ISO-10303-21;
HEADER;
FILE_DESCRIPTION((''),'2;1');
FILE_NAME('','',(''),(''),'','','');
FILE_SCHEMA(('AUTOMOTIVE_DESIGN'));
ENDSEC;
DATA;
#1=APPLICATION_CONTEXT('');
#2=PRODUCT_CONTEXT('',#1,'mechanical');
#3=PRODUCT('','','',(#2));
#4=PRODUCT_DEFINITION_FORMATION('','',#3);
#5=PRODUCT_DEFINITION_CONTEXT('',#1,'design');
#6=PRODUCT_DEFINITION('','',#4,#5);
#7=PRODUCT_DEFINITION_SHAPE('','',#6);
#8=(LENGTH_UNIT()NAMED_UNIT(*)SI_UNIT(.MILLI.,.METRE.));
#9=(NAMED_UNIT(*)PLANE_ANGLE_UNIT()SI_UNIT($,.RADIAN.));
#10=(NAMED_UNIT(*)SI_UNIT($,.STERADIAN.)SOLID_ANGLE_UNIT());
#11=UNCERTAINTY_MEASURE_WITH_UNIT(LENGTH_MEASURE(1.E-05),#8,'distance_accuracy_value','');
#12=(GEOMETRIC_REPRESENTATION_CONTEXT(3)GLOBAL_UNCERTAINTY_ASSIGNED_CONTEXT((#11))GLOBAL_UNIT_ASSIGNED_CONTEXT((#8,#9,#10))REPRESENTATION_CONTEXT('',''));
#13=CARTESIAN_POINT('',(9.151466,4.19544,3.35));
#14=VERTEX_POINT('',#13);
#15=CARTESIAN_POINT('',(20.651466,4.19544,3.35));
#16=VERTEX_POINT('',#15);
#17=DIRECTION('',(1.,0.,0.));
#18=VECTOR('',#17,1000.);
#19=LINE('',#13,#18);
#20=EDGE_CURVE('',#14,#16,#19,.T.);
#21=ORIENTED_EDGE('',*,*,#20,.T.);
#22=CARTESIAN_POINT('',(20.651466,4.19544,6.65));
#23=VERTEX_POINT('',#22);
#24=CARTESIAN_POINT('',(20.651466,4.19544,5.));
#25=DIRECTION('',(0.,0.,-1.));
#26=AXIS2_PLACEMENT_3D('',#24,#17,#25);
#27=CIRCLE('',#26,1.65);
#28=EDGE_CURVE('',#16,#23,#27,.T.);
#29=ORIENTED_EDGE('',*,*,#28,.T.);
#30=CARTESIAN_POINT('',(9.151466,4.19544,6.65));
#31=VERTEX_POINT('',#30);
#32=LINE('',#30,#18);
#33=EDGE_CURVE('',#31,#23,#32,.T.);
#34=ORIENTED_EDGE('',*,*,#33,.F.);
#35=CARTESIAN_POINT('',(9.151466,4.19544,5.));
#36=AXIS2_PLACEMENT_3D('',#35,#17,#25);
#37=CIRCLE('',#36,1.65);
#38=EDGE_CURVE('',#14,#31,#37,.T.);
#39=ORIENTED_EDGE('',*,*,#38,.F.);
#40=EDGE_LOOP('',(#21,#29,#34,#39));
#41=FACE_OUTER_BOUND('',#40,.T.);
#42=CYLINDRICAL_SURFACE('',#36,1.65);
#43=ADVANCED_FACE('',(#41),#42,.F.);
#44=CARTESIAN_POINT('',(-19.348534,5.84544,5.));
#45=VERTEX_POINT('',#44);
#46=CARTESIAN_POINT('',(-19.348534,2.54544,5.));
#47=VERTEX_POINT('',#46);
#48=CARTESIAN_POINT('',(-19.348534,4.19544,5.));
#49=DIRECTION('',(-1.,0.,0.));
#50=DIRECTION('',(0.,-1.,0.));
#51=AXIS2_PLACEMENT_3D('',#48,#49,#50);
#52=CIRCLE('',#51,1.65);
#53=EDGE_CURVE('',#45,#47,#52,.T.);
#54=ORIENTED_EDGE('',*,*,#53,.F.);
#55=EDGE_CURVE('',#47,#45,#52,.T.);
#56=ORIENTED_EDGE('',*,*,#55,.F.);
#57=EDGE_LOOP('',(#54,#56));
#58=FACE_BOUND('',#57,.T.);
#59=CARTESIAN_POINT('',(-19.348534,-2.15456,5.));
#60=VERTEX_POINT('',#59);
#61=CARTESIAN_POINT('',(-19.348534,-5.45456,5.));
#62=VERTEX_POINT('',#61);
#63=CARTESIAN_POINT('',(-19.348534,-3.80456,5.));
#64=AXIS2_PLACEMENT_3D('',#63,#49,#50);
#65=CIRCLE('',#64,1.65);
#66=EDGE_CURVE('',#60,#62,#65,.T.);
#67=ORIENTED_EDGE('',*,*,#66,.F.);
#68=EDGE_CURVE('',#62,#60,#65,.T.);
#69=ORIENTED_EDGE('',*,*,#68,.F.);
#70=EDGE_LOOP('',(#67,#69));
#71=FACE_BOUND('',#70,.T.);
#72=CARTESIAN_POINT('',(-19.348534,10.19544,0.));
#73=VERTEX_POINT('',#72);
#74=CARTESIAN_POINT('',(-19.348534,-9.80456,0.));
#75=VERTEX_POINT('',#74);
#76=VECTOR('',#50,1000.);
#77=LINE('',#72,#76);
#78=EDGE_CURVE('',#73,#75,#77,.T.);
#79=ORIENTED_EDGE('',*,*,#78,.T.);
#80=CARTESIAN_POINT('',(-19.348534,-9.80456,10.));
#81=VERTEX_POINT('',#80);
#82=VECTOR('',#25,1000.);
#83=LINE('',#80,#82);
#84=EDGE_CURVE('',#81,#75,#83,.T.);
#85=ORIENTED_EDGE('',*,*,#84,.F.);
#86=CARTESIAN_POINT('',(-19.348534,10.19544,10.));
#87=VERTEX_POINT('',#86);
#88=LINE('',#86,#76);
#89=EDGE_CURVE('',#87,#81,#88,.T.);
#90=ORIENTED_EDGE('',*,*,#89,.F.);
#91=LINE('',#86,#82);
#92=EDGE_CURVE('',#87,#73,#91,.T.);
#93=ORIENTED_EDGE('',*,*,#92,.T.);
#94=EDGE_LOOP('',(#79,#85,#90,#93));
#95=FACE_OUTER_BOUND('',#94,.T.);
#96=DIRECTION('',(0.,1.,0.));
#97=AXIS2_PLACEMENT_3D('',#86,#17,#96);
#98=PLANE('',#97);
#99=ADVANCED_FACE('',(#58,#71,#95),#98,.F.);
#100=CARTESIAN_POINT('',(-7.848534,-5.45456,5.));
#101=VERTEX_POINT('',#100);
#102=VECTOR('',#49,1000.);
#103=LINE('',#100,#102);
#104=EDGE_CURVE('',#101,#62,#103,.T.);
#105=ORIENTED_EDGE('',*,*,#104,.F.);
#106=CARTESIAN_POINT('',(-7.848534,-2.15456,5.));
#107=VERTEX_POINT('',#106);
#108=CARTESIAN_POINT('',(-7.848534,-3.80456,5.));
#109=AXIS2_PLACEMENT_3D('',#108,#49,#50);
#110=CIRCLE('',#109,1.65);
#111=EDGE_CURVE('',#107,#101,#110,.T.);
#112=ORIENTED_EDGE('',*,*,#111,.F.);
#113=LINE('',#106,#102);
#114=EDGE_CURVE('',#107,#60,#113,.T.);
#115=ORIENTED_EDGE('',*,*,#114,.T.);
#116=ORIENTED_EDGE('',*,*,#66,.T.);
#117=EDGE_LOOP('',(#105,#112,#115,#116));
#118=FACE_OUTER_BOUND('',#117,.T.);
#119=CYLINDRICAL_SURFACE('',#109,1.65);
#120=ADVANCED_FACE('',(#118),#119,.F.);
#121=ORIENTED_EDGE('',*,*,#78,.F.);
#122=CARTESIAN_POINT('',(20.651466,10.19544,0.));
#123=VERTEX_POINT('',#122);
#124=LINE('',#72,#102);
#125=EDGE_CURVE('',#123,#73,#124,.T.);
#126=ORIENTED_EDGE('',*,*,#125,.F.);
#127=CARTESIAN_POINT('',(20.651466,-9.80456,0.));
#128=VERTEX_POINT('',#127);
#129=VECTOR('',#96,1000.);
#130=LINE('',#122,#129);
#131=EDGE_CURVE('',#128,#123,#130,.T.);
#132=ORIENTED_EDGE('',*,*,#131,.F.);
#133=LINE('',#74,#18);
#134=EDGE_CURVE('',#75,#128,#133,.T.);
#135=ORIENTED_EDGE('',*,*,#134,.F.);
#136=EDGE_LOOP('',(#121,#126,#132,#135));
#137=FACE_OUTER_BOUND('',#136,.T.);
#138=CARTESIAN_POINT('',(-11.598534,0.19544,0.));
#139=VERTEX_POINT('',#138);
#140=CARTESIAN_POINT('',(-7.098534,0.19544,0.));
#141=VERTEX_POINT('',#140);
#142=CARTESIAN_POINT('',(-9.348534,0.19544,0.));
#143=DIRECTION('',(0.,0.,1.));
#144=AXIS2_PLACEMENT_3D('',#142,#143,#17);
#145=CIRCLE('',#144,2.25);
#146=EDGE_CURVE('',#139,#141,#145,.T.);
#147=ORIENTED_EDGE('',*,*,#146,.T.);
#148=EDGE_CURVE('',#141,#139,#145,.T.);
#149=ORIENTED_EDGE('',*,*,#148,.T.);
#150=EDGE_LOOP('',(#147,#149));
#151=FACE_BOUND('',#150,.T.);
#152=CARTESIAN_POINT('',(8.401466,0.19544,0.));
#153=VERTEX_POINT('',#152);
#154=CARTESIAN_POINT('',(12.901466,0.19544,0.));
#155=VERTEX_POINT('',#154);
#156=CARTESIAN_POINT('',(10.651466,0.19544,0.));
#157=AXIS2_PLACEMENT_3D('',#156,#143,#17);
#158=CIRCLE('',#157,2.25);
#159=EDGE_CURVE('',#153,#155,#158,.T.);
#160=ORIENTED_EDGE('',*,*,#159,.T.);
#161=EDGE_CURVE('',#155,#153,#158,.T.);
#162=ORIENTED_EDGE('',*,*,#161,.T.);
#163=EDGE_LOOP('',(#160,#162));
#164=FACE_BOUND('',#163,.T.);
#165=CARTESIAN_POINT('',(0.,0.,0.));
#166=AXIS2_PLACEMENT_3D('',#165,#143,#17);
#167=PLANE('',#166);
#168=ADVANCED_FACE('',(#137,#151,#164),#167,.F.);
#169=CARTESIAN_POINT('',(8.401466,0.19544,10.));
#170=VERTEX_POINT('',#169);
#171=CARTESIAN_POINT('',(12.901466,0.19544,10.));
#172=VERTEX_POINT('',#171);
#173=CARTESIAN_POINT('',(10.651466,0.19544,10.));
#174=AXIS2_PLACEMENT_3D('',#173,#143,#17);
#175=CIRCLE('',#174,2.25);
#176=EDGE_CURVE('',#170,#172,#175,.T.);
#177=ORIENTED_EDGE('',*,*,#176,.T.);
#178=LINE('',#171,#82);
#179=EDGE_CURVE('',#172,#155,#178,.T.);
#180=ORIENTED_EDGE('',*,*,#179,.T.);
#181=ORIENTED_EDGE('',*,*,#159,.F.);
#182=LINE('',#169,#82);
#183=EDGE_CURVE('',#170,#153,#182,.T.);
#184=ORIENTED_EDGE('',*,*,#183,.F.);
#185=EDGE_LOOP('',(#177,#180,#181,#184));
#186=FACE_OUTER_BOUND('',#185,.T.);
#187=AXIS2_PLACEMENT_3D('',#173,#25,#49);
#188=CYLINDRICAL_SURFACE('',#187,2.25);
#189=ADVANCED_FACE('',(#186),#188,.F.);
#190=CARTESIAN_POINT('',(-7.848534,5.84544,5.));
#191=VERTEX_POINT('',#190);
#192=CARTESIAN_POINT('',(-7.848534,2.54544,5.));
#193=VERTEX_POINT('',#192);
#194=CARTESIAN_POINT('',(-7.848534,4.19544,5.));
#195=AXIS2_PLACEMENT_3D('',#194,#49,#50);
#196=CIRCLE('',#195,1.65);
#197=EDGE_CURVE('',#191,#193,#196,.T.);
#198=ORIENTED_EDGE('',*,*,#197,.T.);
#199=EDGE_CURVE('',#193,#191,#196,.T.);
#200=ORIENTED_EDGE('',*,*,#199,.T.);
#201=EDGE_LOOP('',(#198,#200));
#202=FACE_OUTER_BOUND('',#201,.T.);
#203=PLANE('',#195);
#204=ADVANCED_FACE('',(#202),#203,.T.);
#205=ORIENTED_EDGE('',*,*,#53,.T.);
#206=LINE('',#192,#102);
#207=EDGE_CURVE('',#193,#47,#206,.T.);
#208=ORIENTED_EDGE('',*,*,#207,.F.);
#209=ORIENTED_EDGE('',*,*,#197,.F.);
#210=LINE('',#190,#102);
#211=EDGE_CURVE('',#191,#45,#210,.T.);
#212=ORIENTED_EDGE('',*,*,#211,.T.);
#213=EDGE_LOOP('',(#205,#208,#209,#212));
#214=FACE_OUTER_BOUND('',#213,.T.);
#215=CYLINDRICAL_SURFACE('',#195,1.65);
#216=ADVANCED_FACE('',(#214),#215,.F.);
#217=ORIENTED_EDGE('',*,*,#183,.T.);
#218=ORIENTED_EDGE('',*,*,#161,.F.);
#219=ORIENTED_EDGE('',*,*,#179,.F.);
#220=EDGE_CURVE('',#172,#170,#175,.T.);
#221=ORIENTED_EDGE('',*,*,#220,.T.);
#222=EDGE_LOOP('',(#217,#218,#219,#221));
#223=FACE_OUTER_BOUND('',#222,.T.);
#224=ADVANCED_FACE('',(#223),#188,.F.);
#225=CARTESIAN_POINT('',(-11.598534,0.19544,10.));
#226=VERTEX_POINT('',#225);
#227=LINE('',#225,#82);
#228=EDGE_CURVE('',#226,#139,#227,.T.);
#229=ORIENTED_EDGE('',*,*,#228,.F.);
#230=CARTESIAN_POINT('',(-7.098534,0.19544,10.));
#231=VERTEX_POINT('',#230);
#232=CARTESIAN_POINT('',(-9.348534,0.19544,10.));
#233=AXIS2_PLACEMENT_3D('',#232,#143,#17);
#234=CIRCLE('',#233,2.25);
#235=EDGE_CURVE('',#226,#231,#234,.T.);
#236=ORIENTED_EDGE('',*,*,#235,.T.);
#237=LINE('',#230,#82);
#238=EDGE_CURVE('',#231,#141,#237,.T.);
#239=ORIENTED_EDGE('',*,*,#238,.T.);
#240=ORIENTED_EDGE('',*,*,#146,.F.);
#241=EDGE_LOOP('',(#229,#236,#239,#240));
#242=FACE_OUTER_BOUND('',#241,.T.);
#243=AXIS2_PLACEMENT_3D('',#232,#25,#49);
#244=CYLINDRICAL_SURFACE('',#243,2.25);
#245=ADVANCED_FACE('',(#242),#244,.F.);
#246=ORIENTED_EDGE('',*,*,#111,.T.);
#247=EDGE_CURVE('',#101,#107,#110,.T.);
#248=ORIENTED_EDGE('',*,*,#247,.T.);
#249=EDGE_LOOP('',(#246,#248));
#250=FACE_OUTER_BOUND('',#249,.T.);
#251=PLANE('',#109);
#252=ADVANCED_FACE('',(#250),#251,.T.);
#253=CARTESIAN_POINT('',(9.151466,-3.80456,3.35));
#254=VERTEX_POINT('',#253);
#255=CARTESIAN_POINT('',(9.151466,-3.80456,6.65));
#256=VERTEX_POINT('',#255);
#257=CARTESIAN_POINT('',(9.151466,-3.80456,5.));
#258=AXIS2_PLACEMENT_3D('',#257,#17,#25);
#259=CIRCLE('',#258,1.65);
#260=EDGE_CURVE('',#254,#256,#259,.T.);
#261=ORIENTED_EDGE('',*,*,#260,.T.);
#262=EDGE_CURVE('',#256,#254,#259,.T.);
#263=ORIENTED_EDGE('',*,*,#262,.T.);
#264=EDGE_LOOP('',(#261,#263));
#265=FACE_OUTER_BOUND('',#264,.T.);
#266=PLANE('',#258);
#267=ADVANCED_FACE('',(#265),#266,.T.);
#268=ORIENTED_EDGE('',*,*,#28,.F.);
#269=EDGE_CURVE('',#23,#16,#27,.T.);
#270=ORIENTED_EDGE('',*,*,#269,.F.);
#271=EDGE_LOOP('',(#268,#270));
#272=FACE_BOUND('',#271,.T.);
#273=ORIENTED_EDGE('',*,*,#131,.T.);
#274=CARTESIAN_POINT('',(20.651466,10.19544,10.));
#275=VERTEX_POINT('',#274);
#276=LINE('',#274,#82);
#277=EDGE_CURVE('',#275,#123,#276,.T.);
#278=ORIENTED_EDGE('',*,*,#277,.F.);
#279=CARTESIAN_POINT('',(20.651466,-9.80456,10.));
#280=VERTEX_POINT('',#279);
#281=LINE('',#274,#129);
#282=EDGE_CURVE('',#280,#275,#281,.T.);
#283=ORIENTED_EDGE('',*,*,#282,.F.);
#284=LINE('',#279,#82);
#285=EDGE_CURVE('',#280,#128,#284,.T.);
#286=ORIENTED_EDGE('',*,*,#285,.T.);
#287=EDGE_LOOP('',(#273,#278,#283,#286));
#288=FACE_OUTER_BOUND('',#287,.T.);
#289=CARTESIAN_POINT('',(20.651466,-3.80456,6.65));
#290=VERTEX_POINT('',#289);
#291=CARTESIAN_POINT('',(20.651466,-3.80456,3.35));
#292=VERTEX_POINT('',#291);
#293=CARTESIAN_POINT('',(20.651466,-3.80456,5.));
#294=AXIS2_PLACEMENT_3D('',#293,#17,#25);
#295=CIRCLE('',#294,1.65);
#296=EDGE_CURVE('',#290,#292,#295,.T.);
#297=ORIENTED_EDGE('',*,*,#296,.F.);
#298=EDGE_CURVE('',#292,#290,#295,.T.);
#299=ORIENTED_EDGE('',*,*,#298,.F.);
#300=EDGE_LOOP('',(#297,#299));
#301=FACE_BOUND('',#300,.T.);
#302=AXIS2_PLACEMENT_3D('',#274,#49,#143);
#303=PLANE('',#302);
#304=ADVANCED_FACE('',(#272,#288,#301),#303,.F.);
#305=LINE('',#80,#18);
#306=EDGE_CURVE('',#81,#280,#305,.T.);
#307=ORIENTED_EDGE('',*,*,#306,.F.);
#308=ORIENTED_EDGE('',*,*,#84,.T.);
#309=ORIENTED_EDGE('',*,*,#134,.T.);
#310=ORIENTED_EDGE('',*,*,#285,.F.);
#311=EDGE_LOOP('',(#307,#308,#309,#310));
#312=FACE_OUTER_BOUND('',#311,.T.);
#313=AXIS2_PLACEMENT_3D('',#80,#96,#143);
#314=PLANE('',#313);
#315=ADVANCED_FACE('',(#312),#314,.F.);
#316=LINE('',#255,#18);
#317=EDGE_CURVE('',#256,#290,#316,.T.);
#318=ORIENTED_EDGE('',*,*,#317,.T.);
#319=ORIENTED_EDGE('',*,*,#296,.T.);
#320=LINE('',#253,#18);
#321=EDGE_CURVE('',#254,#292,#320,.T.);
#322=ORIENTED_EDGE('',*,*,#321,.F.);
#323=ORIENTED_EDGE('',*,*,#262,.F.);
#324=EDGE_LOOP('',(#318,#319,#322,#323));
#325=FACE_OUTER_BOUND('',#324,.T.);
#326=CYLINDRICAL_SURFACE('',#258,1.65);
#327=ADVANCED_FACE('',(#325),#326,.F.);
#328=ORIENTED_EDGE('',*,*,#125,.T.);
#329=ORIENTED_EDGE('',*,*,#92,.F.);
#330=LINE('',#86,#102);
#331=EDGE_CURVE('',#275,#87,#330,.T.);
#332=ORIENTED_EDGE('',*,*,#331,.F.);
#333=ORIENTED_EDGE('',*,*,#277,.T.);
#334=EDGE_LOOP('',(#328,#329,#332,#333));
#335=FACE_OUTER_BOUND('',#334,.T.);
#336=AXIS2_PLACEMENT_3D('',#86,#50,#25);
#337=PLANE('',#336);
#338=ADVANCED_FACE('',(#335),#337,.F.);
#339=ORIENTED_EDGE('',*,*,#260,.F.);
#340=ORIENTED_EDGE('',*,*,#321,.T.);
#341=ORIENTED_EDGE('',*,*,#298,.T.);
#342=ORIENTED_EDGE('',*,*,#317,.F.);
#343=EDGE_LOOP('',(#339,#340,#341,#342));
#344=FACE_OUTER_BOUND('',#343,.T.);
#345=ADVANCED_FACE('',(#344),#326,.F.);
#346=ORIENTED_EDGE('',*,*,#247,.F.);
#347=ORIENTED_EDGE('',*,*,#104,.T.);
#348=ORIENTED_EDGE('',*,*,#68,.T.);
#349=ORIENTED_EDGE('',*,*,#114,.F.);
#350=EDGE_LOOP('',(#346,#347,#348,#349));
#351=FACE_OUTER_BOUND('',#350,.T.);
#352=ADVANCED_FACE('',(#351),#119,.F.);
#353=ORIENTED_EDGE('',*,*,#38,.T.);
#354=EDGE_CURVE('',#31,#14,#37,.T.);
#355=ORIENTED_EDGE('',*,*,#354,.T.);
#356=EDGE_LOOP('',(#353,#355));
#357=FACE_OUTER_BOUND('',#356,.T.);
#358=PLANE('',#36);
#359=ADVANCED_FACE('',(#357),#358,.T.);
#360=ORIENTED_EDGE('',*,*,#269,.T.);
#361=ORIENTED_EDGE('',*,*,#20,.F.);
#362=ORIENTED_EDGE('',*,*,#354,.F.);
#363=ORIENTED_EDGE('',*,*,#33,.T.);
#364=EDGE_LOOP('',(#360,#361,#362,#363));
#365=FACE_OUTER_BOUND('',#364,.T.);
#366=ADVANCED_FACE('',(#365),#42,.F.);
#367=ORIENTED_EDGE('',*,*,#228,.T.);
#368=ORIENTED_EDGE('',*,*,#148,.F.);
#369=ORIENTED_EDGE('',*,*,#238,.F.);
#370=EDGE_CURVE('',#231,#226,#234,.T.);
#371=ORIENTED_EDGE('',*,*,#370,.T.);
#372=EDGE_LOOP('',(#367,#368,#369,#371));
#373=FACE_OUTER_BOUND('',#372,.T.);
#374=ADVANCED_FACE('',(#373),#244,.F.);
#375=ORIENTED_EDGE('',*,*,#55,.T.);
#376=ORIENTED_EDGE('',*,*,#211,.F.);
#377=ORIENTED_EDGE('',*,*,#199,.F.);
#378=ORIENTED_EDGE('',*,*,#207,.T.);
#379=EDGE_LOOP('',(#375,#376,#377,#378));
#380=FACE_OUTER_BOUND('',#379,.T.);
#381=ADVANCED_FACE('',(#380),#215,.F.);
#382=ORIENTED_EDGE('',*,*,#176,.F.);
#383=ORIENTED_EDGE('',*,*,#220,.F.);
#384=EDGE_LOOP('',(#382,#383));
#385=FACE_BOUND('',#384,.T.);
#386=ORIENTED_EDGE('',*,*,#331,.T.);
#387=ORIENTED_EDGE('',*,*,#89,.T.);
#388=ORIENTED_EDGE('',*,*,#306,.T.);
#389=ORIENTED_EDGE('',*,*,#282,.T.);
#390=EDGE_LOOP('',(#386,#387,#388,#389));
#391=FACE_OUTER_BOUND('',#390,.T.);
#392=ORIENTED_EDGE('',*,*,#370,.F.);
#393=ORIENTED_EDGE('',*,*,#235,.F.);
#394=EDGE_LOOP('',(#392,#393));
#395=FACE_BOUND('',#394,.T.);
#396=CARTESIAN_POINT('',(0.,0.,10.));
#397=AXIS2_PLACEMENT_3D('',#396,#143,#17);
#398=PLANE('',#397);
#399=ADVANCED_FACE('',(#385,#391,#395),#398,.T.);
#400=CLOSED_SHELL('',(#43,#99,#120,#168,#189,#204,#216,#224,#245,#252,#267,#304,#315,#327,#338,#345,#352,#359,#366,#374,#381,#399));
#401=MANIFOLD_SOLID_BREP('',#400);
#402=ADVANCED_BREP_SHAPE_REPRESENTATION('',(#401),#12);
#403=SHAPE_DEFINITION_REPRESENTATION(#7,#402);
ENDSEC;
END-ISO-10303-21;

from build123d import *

# Parameters (mm, degrees)
SKETCH_1_W          = 40
SKETCH_1_H          = 20
SKETCH_1_R          = 2.25
EXTRUDE_1_DEPTH     = 10
SKETCH_3_R          = 1.65
CUT_EXTRUDE_1_DEPTH = 11.5
CUT_EXTRUDE_START   = -11.5
SKETCH_4_R          = 1.65
CUT_EXTRUDE_2_DEPTH = 11.5


with BuildPart() as part:
    # 草图1 → 凸台-拉伸1 (new body)
    with BuildSketch(Plane.XY):
        with Locations((0.651465798, 0.195439739)):
            Rectangle(SKETCH_1_W, SKETCH_1_H)
        with Locations((-9.348534202, 0.195439739)):
            Circle(SKETCH_1_R, mode=Mode.SUBTRACT)
        with Locations((10.651465798, 0.195439739)):
            Circle(SKETCH_1_R, mode=Mode.SUBTRACT)
    extrude(amount=EXTRUDE_1_DEPTH)

    # 草图3 → 切除-拉伸1 (cut)
    with BuildSketch(Plane.ZY.offset(19.348534202)):
        with Locations(Location((5, 4.195439739, 0), (0, 0, 270))):
            Circle(SKETCH_3_R)
        with Locations(Location((5, -3.804560261, 0), (0, 0, 270))):
            Circle(SKETCH_3_R)
    extrude(amount=-CUT_EXTRUDE_1_DEPTH, mode=Mode.SUBTRACT)

    # 草图4 → 切除-拉伸2 (cut)
    with BuildSketch(Plane(origin=(20.651465798, 0, 0), x_dir=(0, 0, -1), z_dir=(1, 0, 0)).offset(CUT_EXTRUDE_START)):
        with Locations(Location((-5, 4.195439739, 0), (0, 0, 270))):
            Circle(SKETCH_4_R)
        with Locations(Location((-5, -3.804560261, 0), (0, 0, 270))):
            Circle(SKETCH_4_R)
    extrude(amount=CUT_EXTRUDE_2_DEPTH, mode=Mode.SUBTRACT)


solid = part.part
